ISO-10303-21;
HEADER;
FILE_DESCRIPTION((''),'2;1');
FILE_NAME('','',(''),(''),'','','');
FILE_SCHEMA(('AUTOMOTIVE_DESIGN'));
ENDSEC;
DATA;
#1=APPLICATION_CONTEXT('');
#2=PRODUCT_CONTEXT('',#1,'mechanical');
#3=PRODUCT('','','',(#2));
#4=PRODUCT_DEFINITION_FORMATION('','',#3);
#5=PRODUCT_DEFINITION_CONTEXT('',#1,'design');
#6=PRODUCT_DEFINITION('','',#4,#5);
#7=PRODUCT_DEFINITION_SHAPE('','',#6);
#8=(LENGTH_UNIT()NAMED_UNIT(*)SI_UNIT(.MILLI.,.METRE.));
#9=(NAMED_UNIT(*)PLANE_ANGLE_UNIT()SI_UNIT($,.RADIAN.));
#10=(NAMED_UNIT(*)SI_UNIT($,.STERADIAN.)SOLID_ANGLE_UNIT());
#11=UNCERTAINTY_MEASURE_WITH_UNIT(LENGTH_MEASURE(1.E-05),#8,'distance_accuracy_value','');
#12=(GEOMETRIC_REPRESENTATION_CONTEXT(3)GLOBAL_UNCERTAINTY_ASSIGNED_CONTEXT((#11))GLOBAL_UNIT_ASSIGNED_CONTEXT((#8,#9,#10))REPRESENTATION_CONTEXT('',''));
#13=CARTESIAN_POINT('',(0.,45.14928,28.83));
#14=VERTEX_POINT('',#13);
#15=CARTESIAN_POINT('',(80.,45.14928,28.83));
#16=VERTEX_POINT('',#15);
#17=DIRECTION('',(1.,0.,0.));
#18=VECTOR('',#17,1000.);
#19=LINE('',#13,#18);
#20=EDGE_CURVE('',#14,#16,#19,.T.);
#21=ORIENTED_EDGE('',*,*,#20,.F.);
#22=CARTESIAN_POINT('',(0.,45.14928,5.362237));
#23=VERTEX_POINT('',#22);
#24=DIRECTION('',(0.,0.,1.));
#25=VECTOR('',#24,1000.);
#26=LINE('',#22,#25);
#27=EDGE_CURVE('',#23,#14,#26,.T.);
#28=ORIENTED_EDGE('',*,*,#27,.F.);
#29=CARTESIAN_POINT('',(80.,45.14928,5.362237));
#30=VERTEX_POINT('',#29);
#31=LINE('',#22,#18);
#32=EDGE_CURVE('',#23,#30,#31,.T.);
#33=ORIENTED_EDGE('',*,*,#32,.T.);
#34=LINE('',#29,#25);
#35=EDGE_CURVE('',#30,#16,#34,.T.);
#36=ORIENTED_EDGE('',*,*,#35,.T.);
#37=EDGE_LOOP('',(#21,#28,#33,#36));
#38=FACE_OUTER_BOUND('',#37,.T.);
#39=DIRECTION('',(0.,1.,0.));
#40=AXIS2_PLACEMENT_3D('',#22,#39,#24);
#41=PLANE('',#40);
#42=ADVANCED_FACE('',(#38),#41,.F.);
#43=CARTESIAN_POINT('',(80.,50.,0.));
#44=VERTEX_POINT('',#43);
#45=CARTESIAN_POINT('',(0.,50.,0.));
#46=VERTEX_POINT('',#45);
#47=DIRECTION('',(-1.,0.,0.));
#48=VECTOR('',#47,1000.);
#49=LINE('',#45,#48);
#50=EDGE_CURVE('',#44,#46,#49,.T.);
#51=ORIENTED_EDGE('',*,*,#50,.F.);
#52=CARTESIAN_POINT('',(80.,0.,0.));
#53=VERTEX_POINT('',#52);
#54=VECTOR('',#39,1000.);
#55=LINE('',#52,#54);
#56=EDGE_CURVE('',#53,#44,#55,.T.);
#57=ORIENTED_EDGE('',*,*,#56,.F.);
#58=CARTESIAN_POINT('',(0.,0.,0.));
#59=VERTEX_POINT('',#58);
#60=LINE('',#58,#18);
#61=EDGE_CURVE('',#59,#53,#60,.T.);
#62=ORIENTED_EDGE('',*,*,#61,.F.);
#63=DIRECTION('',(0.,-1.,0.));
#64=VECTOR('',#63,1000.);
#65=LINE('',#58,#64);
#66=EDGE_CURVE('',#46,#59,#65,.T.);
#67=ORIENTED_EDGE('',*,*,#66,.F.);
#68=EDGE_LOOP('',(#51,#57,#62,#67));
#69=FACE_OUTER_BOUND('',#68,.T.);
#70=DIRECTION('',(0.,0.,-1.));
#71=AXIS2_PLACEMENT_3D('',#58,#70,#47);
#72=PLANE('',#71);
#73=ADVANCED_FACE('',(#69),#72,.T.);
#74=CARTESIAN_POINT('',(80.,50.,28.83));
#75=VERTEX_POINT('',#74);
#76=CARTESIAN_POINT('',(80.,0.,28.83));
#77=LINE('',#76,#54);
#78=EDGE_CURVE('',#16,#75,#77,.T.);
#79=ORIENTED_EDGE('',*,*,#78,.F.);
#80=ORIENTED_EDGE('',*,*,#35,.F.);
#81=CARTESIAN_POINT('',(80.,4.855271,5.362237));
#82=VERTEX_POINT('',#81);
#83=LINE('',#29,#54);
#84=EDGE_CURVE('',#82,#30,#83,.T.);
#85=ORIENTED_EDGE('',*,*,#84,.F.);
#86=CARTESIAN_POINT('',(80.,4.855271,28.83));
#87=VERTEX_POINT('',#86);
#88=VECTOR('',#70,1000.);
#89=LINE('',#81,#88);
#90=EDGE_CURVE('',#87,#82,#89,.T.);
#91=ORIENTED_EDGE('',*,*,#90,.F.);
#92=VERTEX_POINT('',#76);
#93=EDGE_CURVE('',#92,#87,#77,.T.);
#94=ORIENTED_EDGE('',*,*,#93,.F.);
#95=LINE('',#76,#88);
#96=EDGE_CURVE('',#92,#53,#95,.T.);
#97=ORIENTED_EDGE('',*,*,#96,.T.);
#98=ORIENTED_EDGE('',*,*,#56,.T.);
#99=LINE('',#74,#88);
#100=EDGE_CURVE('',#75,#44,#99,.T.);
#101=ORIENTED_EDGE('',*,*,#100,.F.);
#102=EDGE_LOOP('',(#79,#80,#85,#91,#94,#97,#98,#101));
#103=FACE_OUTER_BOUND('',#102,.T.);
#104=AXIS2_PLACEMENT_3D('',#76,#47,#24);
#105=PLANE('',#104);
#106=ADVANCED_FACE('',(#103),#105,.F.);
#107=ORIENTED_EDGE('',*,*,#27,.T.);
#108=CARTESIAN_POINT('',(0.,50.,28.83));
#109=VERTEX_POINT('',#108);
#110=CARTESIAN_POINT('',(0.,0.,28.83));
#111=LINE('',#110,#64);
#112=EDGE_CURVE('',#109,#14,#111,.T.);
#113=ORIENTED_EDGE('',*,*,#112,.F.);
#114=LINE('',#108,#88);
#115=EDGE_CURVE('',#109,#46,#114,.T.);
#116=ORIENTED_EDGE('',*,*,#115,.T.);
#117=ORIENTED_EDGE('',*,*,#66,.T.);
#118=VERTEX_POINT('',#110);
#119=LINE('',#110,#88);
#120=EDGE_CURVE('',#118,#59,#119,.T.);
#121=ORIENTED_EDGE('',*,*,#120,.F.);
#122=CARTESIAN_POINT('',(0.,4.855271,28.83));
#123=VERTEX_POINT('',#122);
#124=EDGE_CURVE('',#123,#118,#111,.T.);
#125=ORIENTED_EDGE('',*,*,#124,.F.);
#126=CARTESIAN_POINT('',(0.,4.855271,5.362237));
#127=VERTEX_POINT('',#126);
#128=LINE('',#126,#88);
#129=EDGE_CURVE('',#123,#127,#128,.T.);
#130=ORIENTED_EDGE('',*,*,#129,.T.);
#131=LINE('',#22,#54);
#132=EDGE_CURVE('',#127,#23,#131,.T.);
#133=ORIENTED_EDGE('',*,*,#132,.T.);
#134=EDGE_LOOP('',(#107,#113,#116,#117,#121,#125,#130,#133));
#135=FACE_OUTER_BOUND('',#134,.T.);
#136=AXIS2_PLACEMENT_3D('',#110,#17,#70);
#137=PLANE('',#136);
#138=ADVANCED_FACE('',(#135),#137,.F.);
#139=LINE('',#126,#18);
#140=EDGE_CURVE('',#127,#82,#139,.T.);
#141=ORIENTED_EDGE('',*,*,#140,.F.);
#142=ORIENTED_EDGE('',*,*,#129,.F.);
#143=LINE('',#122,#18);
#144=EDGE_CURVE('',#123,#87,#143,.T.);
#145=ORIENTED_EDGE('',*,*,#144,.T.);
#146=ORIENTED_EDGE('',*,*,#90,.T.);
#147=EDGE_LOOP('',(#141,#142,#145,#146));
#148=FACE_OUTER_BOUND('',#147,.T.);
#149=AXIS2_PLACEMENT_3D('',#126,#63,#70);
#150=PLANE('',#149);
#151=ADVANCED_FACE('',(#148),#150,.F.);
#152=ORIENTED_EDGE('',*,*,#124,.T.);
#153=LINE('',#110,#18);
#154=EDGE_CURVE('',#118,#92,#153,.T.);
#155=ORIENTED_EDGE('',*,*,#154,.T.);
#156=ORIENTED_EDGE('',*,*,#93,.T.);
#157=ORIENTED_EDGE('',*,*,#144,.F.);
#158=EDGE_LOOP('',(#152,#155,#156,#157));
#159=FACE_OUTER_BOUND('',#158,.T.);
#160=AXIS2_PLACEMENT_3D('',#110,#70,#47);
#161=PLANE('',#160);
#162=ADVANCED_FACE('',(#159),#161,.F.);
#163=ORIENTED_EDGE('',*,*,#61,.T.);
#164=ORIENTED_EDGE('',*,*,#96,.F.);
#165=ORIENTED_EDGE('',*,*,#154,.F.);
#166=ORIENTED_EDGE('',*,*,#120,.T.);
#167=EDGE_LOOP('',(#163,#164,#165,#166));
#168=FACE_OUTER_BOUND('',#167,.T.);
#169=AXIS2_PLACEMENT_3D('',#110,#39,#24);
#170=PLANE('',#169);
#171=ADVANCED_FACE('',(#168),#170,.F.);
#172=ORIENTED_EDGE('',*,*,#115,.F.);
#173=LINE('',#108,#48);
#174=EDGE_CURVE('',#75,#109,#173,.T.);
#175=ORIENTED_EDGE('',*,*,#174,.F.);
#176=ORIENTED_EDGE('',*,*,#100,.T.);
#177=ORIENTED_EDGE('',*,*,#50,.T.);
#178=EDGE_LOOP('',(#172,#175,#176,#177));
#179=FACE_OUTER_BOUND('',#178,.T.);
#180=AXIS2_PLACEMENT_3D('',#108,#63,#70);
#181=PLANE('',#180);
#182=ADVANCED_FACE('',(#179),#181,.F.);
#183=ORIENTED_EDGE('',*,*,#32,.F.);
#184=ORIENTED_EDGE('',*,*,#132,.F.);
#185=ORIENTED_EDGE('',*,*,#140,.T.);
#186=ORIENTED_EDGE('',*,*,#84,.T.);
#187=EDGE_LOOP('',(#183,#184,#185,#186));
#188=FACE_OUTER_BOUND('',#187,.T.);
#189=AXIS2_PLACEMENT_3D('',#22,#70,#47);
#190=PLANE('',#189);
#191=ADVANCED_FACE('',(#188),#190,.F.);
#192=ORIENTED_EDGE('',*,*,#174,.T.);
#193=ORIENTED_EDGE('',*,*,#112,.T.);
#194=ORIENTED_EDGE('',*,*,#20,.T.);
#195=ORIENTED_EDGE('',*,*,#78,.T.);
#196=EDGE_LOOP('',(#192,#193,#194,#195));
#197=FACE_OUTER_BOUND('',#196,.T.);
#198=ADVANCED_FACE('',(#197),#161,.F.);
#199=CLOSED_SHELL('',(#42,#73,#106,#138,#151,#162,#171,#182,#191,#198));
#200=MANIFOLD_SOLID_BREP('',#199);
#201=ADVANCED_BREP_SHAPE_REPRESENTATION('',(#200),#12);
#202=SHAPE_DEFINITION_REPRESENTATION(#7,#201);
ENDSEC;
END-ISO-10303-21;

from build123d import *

# Parameters (mm, degrees)
SKETCH1_W           = 80
SKETCH1_H           = 50
BOSS_EXTRUDE1_DEPTH = 28.83
SKETCH2_W           = 23.467762578
SKETCH2_H           = 40.294008895
CUT_EXTRUDE1_DEPTH  = 99.646687223


with BuildPart() as part:
    # Sketch1 → Boss-Extrude1 (new body)
    with BuildSketch(Plane.XY):
        with Locations((40, 25)):
            Rectangle(SKETCH1_W, SKETCH1_H)
    extrude(amount=BOSS_EXTRUDE1_DEPTH)

    # Sketch2 → Cut-Extrude1 (cut, through all)
    with BuildSketch(Plane(origin=(80, 0, 0), x_dir=(0, 0, -1), z_dir=(1, 0, 0))):
        with Locations((-17.096118711, 25.002275375)):
            Rectangle(SKETCH2_W, SKETCH2_H)
    extrude(amount=-CUT_EXTRUDE1_DEPTH, mode=Mode.SUBTRACT)


solid = part.part
